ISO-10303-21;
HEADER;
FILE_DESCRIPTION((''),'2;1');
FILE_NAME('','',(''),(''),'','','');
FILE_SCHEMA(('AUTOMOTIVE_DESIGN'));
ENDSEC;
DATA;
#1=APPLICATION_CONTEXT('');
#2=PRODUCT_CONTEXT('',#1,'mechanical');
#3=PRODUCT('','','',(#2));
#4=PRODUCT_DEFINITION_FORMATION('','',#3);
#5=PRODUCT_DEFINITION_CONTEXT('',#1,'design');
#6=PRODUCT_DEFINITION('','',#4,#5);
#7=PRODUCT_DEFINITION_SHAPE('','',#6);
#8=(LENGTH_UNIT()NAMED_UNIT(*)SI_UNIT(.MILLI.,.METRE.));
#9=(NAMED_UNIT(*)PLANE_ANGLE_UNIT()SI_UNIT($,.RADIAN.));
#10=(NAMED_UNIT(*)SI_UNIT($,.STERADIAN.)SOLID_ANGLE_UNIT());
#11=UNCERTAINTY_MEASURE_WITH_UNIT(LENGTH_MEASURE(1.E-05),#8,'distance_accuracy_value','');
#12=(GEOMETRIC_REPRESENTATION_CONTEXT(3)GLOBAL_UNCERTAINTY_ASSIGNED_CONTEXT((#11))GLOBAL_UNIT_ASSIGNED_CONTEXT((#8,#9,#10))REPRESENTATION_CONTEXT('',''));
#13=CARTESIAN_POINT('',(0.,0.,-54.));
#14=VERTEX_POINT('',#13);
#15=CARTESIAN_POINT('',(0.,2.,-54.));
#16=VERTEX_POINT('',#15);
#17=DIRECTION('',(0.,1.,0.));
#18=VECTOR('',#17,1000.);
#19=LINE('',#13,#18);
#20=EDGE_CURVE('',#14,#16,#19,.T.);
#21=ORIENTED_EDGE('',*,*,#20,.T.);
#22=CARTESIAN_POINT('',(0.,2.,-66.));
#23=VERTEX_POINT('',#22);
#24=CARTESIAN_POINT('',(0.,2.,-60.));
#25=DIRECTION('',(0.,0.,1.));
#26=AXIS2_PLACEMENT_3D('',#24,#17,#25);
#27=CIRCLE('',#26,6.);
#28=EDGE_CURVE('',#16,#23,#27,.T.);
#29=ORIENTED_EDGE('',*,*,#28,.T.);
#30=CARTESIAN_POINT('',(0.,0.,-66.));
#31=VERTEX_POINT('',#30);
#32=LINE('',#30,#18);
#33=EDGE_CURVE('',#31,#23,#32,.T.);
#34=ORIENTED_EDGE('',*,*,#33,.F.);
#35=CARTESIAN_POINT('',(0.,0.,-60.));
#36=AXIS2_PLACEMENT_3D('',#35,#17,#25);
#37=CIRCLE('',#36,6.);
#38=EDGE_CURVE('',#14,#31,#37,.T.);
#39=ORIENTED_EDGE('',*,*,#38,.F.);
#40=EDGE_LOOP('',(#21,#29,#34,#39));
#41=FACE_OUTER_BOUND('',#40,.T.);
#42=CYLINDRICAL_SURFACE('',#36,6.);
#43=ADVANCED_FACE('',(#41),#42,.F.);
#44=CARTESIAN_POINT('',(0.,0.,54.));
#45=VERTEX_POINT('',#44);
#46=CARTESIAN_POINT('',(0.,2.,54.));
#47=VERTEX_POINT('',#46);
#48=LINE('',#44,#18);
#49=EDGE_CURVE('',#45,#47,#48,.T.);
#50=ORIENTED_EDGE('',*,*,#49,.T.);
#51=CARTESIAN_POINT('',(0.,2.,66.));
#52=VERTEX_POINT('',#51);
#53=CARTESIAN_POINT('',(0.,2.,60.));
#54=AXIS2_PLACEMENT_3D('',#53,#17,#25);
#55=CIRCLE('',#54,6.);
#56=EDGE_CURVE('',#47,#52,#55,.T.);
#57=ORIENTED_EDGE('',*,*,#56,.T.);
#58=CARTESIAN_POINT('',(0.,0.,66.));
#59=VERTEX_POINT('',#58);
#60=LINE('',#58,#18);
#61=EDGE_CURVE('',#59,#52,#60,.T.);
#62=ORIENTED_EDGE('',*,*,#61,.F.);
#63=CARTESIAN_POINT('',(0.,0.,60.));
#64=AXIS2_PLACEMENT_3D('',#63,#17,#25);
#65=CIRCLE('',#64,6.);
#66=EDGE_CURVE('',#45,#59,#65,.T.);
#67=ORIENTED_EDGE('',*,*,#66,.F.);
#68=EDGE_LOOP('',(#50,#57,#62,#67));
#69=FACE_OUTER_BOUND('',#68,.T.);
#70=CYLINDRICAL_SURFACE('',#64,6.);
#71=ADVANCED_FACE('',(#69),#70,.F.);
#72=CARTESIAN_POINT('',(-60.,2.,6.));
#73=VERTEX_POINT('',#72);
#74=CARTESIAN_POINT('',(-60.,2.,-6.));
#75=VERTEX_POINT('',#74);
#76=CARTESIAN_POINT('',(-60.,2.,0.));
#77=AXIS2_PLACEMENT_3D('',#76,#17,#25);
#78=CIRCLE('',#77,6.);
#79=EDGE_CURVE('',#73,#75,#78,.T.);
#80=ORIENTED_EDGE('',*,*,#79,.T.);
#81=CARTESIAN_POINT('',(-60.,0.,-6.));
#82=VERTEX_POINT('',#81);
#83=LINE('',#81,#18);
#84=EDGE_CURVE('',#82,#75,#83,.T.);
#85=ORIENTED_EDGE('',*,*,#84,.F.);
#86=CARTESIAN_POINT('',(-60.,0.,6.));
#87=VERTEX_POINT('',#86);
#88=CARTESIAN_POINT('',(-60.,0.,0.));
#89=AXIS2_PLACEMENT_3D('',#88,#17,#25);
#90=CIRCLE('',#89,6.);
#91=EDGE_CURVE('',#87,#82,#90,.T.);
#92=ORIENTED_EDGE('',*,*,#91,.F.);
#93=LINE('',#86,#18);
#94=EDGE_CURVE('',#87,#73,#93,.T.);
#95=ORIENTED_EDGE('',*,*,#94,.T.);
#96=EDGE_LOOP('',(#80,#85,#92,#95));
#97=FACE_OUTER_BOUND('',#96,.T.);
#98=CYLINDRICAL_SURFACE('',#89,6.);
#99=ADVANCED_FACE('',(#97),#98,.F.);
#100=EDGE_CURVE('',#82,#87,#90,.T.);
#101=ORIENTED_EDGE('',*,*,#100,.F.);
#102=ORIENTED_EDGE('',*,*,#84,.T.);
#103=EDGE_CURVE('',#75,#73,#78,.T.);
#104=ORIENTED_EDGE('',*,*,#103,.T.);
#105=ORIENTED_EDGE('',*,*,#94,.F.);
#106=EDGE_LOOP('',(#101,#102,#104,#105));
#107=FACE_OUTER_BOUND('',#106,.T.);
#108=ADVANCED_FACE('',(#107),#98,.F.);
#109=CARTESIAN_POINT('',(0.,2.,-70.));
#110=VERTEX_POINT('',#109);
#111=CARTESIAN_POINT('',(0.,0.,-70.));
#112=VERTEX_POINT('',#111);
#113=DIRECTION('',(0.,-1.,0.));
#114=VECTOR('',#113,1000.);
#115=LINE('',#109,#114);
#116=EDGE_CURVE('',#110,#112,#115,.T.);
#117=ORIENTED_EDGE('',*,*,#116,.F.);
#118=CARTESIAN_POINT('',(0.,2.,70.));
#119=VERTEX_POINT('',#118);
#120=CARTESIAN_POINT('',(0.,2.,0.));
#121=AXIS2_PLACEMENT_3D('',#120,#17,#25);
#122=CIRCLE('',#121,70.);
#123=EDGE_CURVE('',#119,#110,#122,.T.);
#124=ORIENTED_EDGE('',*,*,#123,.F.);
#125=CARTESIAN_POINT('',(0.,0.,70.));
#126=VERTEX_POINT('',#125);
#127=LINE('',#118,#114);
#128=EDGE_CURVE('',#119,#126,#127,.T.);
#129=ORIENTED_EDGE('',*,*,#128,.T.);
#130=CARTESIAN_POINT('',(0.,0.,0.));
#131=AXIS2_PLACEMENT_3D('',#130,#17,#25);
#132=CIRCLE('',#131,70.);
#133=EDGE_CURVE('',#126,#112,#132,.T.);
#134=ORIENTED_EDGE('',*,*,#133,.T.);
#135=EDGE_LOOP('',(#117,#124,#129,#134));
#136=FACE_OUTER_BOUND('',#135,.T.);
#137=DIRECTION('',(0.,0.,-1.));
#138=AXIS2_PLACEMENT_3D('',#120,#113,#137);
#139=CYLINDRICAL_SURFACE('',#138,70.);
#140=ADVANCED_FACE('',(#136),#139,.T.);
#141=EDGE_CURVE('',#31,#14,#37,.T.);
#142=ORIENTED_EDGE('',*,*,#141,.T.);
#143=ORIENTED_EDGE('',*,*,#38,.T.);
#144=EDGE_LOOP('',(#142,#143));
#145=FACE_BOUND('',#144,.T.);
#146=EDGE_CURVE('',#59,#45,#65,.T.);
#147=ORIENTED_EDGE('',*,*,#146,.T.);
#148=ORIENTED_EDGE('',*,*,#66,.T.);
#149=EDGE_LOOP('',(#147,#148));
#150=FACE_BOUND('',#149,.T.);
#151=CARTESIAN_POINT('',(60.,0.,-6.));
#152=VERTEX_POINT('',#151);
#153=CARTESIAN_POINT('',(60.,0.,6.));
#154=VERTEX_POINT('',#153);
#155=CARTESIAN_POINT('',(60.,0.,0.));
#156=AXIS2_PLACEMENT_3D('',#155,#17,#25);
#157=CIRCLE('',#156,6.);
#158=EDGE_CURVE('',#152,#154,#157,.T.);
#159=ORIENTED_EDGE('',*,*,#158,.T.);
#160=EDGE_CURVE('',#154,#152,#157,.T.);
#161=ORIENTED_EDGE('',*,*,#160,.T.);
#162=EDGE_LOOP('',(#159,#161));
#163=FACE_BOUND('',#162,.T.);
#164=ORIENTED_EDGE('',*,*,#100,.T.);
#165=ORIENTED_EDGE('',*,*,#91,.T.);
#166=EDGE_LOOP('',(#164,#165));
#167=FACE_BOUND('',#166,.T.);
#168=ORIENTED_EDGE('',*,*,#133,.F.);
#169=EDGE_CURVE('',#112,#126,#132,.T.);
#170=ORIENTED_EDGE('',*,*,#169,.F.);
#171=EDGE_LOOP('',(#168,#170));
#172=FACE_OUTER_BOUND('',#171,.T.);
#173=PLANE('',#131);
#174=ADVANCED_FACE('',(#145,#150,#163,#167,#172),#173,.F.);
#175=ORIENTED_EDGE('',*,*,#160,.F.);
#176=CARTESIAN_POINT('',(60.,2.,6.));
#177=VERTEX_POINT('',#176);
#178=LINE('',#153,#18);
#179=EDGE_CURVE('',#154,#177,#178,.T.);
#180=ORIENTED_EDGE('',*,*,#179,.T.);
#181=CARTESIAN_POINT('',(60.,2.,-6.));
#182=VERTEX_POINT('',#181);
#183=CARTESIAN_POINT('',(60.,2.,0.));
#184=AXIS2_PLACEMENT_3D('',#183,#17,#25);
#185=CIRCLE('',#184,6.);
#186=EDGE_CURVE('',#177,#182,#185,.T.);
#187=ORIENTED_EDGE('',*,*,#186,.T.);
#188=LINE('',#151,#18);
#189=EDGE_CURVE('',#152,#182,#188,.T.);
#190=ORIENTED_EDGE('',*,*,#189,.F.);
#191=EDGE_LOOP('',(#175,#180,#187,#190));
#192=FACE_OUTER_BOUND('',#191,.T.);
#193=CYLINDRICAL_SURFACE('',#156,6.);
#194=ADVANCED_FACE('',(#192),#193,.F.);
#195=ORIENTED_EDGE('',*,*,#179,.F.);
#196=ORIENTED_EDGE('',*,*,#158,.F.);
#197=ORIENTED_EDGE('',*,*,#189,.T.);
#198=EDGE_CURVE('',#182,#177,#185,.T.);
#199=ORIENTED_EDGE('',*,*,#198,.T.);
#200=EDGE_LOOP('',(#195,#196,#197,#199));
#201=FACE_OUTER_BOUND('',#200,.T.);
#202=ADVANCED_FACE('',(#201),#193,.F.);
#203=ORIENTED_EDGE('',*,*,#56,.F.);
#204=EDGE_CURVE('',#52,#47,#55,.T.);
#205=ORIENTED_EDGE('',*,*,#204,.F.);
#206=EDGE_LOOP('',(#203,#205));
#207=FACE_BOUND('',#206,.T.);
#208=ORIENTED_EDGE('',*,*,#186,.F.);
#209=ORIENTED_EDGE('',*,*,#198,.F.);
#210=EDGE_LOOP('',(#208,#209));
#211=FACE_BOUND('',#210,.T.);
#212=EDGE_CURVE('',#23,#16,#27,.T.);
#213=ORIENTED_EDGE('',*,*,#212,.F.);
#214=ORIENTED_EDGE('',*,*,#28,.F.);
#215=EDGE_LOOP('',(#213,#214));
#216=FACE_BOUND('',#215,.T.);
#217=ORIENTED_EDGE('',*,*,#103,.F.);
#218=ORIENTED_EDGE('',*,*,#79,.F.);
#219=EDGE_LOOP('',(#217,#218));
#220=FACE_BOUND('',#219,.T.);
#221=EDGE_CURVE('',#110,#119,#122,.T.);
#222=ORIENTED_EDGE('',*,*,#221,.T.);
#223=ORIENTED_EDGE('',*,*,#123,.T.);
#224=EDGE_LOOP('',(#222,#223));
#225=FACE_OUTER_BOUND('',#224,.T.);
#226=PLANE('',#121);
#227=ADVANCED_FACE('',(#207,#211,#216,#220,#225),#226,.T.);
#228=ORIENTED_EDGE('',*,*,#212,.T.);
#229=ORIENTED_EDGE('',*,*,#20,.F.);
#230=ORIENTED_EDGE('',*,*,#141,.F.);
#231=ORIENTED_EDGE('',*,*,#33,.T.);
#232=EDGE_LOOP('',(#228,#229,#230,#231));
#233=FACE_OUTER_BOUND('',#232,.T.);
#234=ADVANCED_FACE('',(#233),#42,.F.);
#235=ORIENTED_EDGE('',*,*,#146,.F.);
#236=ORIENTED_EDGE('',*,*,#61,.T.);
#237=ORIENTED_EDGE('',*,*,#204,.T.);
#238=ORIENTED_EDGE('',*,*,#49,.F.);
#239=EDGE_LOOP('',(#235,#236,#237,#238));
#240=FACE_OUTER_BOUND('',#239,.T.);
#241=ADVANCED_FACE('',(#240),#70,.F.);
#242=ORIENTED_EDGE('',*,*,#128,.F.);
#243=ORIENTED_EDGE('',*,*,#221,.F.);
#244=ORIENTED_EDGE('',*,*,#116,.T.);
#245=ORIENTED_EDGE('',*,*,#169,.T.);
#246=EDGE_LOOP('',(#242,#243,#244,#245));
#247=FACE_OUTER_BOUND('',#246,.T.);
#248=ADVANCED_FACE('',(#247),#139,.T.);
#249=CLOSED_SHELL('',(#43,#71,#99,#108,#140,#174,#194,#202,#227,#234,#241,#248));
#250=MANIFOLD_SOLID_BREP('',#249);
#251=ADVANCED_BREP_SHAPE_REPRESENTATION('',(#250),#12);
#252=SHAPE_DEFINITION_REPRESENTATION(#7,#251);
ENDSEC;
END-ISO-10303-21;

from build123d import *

# Parameters (mm, degrees)
SKETCH_1_R          = 70
EXTRUDE_1_DEPTH     = 2
SKETCH_3_R          = 6
CUT_EXTRUDE_1_DEPTH = 100.015150356


with BuildPart() as part:
    # 草图1 → 凸台-拉伸1 (new body)
    with BuildSketch(Plane(origin=(0, 0, 0), x_dir=(1, 0, 0), z_dir=(0, 1, 0))):
        with Locations(Location((0, 0, 0), (0, 0, 270))):
            Circle(SKETCH_1_R)
    extrude(amount=EXTRUDE_1_DEPTH)

    # 草图3 → 切除-拉伸1 (cut, through all)
    with BuildSketch(Plane(origin=(0, 2, 0), x_dir=(1, 0, 0), z_dir=(0, 1, 0))):
        with Locations(Location((0, 60, 0), (0, 0, 270))):
            Circle(SKETCH_3_R)
        with Locations(Location((60, 0, 0), (0, 0, 270))):
            Circle(SKETCH_3_R)
        with Locations(Location((0, -60, 0), (0, 0, 270))):
            Circle(SKETCH_3_R)
        with Locations(Location((-60, 0, 0), (0, 0, 270))):
            Circle(SKETCH_3_R)
    extrude(amount=-CUT_EXTRUDE_1_DEPTH, mode=Mode.SUBTRACT)


solid = part.part
